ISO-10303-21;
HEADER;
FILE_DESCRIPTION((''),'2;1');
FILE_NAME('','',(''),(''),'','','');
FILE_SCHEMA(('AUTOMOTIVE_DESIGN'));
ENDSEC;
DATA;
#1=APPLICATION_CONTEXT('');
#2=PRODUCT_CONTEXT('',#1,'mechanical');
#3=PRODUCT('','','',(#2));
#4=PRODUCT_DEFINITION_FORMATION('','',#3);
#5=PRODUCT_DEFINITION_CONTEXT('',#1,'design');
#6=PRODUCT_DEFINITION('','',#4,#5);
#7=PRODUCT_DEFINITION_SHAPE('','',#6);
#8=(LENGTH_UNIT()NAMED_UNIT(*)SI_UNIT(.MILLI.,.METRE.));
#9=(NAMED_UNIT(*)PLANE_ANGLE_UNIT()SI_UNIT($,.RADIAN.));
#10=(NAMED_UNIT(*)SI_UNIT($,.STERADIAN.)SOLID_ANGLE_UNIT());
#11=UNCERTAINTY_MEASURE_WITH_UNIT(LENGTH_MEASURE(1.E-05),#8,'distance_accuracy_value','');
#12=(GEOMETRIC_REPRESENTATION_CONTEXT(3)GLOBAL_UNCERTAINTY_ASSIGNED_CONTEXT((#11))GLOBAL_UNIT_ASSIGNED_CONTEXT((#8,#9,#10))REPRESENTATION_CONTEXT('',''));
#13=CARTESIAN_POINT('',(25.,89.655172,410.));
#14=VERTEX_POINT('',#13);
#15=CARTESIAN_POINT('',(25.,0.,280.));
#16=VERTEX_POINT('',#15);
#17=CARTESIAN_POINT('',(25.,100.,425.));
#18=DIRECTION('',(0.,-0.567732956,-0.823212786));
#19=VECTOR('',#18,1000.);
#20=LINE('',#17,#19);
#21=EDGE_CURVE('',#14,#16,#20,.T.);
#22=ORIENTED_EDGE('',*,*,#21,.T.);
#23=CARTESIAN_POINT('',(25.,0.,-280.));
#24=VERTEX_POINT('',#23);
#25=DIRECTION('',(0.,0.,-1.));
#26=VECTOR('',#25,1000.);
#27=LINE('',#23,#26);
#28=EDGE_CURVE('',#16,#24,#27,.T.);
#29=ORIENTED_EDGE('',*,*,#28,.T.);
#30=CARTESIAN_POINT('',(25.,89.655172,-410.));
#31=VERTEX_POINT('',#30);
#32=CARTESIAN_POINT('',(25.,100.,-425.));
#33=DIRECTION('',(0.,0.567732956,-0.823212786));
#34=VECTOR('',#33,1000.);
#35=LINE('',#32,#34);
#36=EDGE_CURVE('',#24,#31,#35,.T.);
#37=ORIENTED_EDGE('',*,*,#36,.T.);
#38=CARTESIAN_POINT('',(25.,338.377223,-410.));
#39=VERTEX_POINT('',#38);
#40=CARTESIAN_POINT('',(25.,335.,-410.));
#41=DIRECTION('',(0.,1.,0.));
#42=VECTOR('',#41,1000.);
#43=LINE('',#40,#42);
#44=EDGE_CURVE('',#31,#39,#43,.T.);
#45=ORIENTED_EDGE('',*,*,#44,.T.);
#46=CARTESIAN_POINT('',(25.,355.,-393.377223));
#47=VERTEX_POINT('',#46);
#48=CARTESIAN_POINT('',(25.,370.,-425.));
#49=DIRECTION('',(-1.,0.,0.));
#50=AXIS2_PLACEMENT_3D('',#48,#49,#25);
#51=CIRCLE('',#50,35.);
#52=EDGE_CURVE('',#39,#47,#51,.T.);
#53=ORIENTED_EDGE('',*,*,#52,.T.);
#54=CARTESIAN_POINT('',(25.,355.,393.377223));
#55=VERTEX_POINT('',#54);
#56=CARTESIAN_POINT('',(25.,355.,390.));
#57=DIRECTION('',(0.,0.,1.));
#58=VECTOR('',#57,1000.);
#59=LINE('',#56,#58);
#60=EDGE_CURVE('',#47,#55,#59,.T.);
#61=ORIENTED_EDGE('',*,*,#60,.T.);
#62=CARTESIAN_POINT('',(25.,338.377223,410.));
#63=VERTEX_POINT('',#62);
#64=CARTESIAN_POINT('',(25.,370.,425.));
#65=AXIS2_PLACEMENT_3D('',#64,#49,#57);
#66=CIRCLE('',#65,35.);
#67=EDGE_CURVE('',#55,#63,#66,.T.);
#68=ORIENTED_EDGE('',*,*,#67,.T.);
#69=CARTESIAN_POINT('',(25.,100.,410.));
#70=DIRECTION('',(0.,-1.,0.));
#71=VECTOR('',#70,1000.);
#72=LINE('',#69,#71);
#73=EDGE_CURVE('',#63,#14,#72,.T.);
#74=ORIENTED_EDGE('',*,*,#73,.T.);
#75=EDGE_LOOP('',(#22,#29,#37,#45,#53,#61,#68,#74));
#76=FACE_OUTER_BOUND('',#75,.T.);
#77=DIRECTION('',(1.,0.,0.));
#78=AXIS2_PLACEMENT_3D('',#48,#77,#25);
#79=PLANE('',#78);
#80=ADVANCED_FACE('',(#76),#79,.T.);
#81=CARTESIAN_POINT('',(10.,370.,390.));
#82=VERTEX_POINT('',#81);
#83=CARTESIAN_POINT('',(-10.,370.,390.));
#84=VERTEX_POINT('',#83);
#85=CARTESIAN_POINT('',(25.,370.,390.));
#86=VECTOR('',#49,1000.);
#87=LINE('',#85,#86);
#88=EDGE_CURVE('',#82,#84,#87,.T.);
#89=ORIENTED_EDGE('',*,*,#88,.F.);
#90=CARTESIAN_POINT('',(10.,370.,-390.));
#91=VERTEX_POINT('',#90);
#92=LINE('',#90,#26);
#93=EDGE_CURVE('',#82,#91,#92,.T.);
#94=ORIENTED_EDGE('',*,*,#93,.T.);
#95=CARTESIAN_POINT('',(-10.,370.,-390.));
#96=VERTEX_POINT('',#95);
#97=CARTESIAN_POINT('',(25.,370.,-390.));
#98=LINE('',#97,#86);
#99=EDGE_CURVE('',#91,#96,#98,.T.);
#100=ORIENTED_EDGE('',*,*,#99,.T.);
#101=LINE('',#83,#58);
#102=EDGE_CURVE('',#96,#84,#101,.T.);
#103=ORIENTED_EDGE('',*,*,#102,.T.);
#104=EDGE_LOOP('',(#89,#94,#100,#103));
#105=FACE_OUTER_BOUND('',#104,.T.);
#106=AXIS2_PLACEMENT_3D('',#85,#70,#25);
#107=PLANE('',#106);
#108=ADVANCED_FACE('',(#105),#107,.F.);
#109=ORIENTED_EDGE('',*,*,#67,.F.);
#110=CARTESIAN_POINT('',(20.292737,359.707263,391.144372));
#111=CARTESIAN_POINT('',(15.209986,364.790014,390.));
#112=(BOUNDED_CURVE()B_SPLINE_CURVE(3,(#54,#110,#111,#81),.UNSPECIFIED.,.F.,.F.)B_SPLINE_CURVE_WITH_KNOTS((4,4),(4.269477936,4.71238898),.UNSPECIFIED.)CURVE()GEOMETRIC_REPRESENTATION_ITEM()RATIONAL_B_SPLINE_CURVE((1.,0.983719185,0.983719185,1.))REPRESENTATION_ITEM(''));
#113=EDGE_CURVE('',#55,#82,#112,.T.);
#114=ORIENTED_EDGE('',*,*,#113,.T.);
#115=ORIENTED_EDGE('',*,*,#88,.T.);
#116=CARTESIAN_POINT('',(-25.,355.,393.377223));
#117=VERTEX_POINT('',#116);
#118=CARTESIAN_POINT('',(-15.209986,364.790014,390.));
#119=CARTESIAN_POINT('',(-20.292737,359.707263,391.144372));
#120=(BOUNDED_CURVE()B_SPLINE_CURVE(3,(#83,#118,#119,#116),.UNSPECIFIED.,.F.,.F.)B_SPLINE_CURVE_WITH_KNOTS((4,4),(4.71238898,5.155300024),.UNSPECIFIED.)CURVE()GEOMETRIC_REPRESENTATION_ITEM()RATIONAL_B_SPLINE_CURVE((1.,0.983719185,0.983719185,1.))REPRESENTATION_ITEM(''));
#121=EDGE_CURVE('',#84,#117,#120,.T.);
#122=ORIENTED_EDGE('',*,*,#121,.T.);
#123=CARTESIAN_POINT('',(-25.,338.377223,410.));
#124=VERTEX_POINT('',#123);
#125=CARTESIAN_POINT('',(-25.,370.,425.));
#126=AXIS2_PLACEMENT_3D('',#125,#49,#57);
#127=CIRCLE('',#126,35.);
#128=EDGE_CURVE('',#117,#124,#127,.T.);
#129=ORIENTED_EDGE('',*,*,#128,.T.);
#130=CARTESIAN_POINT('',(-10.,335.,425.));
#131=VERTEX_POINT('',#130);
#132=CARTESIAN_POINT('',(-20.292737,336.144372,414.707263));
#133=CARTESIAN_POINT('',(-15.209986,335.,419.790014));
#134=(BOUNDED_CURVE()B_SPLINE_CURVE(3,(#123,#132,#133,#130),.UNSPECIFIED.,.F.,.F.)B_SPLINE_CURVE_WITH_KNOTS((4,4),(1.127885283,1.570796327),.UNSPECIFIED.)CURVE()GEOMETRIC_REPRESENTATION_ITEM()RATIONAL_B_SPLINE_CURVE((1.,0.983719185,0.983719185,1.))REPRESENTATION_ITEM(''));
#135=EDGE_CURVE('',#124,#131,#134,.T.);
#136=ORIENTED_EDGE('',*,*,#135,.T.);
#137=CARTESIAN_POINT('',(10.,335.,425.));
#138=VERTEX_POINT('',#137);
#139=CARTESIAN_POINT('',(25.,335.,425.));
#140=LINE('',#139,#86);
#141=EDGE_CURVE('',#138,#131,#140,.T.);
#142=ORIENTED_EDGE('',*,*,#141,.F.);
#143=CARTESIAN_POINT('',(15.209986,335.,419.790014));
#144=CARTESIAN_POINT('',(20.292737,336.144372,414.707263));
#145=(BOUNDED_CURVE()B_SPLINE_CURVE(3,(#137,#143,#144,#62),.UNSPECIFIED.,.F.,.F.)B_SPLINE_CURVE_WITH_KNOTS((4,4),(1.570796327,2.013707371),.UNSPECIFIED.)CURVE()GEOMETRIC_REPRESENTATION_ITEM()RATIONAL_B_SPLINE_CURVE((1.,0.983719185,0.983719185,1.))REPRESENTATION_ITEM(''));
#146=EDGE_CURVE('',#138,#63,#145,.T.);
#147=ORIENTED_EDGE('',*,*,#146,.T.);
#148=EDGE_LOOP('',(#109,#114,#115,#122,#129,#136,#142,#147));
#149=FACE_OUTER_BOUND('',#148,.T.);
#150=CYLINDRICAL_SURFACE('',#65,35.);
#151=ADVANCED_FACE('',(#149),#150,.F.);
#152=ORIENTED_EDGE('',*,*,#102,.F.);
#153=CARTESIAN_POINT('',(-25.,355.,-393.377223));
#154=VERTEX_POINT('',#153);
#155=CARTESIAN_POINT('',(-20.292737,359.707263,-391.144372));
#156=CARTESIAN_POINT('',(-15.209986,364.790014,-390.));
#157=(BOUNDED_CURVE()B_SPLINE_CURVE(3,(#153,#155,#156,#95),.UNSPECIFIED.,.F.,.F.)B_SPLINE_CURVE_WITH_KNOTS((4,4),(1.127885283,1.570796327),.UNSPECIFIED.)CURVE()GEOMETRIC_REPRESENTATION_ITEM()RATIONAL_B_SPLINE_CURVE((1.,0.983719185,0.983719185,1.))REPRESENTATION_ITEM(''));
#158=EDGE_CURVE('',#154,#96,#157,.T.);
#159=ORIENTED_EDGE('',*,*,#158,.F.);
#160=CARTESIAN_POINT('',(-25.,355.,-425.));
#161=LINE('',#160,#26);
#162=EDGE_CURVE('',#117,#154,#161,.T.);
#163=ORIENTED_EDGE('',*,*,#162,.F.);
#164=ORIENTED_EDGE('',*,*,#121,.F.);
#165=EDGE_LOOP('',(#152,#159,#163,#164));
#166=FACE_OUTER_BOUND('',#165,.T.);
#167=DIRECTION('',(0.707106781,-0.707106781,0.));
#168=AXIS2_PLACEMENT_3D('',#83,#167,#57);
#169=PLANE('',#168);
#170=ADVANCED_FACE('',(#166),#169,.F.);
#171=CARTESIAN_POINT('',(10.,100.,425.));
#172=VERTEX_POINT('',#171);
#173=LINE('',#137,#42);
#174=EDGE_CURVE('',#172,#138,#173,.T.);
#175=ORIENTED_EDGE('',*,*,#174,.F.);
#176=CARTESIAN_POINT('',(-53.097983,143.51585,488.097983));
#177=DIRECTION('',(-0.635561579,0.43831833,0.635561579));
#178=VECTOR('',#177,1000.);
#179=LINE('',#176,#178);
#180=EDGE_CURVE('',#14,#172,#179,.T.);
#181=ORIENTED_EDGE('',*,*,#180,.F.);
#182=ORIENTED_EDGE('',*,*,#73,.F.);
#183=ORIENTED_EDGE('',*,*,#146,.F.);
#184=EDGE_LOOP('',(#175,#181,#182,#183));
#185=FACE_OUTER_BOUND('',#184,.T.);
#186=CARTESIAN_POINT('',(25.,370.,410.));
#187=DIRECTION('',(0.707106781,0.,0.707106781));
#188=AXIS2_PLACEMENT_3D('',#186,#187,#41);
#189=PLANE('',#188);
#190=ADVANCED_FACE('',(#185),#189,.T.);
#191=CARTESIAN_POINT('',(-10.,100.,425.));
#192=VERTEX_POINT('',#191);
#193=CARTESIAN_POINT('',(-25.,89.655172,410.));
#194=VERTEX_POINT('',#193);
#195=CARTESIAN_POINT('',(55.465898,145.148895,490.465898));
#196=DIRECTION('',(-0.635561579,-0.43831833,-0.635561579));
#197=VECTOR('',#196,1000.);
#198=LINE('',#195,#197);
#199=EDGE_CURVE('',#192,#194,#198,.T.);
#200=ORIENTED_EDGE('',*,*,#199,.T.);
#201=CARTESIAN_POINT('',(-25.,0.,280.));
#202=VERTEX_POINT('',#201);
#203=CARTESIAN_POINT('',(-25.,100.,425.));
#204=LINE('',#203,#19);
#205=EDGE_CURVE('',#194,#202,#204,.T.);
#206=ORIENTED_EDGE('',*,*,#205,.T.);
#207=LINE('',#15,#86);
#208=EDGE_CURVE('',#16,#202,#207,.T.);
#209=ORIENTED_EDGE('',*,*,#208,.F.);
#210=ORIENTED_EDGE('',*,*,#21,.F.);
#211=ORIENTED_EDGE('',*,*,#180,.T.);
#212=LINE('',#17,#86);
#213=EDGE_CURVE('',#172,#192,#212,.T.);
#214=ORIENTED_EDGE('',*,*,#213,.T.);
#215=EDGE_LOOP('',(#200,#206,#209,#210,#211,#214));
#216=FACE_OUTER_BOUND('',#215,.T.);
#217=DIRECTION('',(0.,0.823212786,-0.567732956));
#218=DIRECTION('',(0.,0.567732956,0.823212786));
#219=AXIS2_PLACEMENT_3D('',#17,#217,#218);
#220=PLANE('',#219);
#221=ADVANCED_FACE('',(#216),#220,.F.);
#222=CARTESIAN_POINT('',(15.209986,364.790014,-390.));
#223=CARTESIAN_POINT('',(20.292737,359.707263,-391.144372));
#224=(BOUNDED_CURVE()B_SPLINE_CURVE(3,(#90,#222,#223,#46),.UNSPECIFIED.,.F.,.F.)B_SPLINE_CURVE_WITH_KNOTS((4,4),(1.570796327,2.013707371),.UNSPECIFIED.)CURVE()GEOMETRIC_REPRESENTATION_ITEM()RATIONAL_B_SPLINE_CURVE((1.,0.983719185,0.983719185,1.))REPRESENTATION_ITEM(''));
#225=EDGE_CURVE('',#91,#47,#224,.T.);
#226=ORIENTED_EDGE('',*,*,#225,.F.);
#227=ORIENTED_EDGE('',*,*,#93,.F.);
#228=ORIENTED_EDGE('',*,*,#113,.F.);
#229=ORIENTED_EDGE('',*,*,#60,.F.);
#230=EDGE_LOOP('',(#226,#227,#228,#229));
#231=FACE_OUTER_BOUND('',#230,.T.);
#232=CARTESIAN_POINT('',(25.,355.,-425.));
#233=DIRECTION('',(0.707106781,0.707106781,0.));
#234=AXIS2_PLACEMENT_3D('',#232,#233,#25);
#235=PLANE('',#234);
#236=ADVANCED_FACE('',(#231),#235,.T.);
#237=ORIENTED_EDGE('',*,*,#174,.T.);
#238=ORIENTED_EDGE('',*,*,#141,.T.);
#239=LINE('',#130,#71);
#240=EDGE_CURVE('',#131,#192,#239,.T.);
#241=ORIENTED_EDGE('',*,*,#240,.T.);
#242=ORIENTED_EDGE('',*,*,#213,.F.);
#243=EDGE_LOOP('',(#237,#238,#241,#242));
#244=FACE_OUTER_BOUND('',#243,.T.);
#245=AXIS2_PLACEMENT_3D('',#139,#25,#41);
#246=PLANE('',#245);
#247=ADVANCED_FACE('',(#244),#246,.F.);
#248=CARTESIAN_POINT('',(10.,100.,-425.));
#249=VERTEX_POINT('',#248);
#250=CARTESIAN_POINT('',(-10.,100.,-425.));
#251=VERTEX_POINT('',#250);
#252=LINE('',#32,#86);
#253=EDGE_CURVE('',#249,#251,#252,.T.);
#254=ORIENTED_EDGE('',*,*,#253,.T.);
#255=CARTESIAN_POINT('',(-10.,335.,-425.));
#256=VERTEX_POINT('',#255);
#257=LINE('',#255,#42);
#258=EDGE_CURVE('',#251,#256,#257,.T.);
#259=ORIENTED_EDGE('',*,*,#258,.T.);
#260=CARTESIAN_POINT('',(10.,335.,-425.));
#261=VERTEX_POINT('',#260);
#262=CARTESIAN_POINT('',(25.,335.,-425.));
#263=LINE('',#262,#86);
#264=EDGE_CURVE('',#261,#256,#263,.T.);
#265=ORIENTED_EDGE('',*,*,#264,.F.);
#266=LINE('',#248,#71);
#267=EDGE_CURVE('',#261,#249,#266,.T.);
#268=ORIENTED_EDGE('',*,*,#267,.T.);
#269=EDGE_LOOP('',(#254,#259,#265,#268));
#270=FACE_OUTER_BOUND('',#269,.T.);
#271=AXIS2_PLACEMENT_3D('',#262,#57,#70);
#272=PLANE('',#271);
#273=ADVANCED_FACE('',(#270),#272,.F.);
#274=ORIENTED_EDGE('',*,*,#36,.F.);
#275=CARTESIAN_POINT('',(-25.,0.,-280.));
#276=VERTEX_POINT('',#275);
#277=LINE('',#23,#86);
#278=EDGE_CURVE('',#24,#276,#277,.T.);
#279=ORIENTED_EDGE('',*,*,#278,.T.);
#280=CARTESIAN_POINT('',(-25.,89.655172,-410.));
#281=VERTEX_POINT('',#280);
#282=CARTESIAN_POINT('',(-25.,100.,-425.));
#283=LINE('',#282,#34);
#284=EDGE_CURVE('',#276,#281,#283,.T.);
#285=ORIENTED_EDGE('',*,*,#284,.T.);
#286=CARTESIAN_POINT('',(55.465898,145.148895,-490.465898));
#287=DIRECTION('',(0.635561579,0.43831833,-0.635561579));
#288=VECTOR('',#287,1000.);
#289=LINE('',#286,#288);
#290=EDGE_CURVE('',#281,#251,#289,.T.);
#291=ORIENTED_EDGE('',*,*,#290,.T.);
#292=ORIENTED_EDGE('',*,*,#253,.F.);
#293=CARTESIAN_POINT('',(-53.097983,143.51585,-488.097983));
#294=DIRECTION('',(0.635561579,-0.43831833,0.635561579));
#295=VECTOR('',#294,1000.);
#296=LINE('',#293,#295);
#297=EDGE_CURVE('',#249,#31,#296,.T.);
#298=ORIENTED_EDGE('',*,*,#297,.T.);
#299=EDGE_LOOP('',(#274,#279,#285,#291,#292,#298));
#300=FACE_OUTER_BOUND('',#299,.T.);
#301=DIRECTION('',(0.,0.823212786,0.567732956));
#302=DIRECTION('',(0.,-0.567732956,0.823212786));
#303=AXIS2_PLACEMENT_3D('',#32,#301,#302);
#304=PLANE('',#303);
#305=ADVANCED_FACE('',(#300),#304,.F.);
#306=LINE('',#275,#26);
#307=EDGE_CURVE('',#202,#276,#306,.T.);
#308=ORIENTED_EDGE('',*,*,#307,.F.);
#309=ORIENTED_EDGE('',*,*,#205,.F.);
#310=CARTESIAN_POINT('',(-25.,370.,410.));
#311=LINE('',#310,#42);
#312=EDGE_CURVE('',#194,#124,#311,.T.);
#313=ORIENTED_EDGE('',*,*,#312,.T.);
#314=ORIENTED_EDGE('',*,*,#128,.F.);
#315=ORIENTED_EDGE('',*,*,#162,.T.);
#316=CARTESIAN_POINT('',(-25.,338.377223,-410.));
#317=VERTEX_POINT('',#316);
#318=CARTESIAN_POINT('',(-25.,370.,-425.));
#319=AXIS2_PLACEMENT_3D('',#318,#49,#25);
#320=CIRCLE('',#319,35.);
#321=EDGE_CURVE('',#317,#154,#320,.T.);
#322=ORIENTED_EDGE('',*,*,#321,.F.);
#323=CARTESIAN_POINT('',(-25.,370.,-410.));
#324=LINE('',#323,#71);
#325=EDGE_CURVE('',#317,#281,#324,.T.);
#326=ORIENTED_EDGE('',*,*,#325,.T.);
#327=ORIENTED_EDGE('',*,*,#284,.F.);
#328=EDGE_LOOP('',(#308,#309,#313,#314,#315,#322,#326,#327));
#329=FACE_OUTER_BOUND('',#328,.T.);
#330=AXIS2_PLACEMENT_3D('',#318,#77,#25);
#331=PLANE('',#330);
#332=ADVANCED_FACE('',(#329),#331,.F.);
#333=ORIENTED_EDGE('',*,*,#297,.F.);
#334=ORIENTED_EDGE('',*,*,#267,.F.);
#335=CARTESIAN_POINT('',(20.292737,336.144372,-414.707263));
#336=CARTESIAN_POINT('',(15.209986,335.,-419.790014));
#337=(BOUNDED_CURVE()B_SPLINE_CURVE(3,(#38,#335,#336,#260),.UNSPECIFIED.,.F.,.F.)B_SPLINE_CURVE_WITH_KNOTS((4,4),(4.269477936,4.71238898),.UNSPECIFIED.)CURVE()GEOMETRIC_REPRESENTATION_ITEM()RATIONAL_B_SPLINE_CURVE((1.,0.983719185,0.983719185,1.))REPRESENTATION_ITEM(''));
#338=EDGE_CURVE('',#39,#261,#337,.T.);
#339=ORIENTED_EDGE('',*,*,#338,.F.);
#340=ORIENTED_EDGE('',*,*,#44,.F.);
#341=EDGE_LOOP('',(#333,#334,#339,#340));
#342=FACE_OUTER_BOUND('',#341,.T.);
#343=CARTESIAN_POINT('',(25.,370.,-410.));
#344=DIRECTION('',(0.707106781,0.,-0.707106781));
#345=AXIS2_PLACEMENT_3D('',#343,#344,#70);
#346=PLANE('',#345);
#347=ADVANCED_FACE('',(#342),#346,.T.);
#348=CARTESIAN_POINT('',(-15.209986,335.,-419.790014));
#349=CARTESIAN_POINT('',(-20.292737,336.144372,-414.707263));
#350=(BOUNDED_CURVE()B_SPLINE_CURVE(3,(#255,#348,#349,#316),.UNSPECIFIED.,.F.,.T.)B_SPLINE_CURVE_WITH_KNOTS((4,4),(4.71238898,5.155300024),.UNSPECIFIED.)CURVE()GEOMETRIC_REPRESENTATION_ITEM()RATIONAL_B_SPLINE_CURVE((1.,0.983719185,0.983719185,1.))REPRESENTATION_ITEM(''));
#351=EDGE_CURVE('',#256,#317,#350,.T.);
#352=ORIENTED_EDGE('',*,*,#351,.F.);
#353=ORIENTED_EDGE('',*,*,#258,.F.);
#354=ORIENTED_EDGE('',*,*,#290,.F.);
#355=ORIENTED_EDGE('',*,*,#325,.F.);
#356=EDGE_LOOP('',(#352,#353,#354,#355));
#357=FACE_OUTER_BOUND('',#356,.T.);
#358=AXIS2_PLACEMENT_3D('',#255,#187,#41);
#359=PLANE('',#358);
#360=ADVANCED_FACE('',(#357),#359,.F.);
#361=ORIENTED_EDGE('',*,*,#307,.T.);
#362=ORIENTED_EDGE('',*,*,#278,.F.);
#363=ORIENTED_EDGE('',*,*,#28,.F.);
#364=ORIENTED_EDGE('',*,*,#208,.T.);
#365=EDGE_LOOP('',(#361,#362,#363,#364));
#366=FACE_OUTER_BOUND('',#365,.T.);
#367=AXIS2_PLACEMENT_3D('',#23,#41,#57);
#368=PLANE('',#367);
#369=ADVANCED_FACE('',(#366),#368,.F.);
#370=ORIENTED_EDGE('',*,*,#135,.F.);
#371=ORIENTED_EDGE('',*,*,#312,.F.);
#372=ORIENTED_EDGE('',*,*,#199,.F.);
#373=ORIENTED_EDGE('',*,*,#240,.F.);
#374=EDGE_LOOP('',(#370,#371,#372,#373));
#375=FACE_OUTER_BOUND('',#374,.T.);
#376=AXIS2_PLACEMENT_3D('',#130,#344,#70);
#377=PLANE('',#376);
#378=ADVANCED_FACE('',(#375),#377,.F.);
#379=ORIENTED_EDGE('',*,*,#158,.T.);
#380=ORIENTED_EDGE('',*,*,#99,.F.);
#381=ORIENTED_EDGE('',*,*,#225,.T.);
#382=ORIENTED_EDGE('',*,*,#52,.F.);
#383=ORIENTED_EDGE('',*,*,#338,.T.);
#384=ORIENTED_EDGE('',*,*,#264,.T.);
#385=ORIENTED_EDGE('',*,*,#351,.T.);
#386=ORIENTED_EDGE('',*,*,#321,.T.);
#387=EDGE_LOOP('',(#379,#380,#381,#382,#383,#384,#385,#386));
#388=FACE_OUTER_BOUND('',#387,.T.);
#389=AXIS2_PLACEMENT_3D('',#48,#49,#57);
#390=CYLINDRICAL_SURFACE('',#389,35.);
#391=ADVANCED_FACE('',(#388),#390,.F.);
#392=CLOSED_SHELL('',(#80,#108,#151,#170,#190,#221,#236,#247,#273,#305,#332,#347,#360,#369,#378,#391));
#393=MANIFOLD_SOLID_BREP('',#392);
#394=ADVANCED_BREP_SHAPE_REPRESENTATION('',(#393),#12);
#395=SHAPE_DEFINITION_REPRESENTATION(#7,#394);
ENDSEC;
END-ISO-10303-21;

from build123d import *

# Parameters (mm, degrees)
BOSS_EXTRUDE1_DEPTH = 25
CHAMFER1_SIZE       = 15


with BuildPart() as part:
    # Sketch1 → Boss-Extrude1 (new, symmetric)
    with BuildSketch(Plane(origin=(0, 0, 0), x_dir=(0, 0, -1), z_dir=(1, 0, 0))):
        with BuildLine():
            Line((-390, 370), (390, 370))
            ThreePointArc((390, 370), (400.251262658, 345.251262658), (425, 335))
            Line((425, 335), (425, 100))
            Line((425, 100), (280, 0))
            Line((280, 0), (-280, 0))
            Line((-280, 0), (-425, 100))
            Line((-425, 100), (-425, 335))
            ThreePointArc((-425, 335), (-400.251262658, 345.251262658), (-390, 370))
        make_face()
    extrude(amount=BOSS_EXTRUDE1_DEPTH, both=True)

    # Chamfer1
    chamfer1_edges = [part.edges().sort_by_distance(p)[0] for p in [
        (-25, 370, 0),
        (25, 217.5, 425),
        (25, 217.5, -425),
        (25, 370, 0),
        (-25, 217.5, -425),
        (-25, 217.5, 425),
    ]]
    chamfer(chamfer1_edges, length=CHAMFER1_SIZE)


solid = part.part
